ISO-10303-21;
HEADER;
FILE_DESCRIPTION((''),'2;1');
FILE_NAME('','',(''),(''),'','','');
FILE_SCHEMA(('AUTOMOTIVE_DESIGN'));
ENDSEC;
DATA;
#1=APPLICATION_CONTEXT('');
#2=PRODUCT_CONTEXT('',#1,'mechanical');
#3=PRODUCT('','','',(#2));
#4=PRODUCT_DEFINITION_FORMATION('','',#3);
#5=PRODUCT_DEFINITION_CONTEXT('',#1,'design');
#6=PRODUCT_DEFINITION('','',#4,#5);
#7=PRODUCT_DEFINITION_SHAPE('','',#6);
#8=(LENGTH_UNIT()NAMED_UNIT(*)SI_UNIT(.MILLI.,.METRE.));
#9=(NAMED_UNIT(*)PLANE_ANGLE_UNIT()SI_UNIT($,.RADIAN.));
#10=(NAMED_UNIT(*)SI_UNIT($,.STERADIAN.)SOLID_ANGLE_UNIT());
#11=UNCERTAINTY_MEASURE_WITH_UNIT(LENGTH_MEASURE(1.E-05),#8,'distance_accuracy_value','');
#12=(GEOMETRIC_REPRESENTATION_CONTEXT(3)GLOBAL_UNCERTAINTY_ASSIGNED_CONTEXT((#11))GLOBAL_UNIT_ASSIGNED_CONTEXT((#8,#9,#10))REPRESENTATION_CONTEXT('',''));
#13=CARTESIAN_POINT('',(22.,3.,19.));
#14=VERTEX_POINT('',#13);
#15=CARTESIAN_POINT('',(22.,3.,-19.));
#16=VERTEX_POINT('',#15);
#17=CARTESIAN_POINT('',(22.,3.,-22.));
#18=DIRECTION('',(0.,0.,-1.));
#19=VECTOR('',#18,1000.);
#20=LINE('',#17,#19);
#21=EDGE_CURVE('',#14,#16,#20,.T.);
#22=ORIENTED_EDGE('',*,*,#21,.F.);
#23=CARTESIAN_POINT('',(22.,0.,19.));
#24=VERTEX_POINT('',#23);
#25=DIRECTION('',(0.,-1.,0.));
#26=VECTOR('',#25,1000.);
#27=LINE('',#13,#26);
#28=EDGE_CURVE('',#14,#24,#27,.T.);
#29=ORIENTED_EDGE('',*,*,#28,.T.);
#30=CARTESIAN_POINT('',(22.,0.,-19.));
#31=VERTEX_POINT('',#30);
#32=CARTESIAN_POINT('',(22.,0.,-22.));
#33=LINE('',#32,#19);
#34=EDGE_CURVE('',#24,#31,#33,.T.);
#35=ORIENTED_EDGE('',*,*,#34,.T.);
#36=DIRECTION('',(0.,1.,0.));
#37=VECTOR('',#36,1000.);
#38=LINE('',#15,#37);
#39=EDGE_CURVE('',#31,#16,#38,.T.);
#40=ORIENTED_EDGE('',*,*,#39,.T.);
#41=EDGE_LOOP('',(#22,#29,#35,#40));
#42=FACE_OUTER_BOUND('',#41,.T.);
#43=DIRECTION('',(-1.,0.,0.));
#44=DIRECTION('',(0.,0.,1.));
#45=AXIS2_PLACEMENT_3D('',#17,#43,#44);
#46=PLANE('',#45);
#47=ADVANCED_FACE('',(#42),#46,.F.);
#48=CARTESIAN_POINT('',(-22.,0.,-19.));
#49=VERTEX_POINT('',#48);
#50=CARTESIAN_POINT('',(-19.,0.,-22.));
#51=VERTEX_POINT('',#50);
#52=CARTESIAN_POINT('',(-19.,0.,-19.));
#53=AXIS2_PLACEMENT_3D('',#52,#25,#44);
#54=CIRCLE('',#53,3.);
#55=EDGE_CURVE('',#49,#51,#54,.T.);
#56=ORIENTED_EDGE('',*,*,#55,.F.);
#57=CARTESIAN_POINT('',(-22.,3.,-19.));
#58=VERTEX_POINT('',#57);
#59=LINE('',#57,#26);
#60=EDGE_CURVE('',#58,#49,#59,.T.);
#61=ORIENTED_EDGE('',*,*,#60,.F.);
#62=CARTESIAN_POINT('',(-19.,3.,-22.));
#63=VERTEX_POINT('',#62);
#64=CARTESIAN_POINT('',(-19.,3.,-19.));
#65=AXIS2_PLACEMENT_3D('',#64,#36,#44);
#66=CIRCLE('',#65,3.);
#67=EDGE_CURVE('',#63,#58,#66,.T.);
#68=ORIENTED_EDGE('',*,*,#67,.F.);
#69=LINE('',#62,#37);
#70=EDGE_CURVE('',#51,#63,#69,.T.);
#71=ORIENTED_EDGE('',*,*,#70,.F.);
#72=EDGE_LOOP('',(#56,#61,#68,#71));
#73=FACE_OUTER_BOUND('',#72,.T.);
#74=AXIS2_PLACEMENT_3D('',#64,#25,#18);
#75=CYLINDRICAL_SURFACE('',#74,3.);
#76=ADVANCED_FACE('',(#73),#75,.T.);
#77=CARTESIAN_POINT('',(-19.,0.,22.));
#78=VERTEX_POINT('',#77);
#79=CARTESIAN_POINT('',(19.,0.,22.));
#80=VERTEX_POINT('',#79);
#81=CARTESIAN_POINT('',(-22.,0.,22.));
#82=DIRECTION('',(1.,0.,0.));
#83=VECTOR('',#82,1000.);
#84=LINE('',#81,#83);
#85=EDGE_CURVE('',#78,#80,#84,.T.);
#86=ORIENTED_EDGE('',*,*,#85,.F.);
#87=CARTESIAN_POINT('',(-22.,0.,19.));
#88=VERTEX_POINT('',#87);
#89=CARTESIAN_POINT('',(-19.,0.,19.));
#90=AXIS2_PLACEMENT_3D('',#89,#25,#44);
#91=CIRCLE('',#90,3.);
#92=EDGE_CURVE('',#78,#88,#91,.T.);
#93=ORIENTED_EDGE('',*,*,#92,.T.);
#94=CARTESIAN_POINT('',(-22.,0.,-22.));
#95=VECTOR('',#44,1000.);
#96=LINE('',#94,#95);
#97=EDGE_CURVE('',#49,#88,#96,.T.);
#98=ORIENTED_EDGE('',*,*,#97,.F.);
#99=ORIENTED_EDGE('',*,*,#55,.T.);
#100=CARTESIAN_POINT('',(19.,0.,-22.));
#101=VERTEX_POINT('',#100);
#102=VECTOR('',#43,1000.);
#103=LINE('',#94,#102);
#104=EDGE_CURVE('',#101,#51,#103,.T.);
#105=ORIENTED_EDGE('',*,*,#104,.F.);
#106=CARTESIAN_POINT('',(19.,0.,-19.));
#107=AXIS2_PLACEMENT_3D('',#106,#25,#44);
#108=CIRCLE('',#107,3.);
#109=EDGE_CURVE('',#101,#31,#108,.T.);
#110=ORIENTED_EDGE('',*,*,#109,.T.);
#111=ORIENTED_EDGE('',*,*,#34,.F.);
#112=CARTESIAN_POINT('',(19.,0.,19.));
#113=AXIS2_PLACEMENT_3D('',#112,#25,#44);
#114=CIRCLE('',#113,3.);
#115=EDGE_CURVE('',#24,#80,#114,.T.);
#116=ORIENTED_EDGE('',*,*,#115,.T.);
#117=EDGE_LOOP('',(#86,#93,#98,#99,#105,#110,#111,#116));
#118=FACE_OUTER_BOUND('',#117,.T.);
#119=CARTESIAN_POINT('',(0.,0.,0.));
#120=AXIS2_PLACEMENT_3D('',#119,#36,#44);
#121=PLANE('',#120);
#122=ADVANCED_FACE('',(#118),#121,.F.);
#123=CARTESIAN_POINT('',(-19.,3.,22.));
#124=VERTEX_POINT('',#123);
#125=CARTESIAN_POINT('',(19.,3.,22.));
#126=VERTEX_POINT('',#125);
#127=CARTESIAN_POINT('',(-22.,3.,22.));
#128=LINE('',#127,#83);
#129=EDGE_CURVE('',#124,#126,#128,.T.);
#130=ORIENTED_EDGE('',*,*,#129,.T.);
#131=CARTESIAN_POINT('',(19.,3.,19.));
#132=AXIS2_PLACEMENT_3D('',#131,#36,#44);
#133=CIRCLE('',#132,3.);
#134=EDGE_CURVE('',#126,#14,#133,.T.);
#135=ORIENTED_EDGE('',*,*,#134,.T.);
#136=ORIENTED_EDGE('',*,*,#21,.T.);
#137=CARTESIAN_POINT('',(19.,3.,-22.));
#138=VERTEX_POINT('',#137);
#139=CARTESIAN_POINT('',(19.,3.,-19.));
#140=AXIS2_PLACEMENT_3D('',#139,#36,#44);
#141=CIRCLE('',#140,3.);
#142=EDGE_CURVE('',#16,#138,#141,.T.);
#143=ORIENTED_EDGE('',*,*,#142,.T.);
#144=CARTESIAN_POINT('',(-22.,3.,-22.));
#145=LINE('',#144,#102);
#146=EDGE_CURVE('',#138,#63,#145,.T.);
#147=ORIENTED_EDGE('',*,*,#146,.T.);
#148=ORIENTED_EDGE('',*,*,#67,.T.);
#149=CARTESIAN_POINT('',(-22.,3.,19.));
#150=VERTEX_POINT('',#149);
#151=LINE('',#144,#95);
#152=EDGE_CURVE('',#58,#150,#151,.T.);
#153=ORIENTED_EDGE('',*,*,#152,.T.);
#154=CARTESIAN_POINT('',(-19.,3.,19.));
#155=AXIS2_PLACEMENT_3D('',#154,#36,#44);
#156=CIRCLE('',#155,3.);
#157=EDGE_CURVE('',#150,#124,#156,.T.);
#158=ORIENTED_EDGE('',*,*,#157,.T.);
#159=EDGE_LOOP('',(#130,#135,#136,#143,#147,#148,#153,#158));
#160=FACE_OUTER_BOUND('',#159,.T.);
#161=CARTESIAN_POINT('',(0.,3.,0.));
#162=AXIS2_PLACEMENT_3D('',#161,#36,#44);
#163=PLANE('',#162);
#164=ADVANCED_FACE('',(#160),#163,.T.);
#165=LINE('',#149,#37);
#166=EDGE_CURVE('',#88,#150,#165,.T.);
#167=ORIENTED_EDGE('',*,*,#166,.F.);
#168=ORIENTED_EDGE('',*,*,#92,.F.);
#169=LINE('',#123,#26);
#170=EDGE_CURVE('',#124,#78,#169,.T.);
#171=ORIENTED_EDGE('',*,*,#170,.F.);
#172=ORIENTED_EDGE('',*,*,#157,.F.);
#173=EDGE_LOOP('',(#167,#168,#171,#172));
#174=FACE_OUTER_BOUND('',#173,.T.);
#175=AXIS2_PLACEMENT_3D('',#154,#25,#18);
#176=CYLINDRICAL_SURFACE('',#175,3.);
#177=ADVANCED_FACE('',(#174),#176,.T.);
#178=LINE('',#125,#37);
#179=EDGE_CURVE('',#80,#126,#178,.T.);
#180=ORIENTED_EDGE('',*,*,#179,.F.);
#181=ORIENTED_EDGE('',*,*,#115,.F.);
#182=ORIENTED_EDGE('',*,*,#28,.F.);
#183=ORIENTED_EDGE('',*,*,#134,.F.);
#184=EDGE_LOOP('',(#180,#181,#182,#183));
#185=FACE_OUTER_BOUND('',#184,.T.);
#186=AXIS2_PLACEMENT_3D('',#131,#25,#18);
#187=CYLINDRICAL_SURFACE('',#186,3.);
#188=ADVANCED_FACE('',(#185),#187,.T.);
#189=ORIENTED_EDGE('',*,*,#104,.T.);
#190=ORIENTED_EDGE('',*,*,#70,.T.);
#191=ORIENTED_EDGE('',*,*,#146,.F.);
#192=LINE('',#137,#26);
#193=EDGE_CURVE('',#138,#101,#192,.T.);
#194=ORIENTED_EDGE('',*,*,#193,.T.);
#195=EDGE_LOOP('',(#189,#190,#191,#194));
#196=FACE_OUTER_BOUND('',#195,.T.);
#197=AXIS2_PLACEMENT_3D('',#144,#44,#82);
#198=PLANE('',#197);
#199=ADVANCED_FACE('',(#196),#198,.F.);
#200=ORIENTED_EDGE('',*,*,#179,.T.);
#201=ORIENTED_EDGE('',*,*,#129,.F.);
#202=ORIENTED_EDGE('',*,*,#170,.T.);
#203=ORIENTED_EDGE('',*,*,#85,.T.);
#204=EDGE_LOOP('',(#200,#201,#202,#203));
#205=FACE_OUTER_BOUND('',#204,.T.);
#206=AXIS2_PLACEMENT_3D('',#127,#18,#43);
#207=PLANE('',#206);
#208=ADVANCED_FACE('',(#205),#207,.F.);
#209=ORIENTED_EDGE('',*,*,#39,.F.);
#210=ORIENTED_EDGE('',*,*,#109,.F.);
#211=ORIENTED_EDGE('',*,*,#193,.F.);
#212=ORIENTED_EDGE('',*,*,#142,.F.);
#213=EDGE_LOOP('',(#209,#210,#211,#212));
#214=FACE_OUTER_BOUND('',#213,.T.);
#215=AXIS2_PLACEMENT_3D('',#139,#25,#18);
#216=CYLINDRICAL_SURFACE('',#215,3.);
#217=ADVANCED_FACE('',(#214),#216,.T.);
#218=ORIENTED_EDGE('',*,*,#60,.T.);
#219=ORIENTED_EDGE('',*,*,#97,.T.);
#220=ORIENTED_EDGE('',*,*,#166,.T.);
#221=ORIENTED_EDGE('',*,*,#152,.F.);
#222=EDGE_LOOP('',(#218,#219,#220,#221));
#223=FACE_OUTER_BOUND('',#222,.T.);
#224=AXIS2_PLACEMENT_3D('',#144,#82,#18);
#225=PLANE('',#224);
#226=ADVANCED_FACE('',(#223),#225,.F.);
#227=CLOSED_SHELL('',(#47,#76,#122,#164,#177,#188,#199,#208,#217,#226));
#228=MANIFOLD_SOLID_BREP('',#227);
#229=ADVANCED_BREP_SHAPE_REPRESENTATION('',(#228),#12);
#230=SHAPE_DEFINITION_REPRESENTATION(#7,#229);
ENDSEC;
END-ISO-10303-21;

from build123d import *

# Parameters (mm, degrees)
SKETCH_1_W      = 44
SKETCH_1_H      = 44
EXTRUDE_1_DEPTH = 3
FILLET_1_R      = 3


with BuildPart() as part:
    # 草图1 → 凸台-拉伸1 (new body)
    with BuildSketch(Plane(origin=(0, 0, 0), x_dir=(1, 0, 0), z_dir=(0, 1, 0))):
        Rectangle(SKETCH_1_W, SKETCH_1_H)
    extrude(amount=EXTRUDE_1_DEPTH)

    # 圆角1
    fillet_1_edges = [part.edges().sort_by_distance(p)[0] for p in [
        (22, 1.5, 22),
        (-22, 1.5, 22),
        (-22, 1.5, -22),
        (22, 1.5, -22),
    ]]
    fillet(fillet_1_edges, radius=FILLET_1_R)


solid = part.part
